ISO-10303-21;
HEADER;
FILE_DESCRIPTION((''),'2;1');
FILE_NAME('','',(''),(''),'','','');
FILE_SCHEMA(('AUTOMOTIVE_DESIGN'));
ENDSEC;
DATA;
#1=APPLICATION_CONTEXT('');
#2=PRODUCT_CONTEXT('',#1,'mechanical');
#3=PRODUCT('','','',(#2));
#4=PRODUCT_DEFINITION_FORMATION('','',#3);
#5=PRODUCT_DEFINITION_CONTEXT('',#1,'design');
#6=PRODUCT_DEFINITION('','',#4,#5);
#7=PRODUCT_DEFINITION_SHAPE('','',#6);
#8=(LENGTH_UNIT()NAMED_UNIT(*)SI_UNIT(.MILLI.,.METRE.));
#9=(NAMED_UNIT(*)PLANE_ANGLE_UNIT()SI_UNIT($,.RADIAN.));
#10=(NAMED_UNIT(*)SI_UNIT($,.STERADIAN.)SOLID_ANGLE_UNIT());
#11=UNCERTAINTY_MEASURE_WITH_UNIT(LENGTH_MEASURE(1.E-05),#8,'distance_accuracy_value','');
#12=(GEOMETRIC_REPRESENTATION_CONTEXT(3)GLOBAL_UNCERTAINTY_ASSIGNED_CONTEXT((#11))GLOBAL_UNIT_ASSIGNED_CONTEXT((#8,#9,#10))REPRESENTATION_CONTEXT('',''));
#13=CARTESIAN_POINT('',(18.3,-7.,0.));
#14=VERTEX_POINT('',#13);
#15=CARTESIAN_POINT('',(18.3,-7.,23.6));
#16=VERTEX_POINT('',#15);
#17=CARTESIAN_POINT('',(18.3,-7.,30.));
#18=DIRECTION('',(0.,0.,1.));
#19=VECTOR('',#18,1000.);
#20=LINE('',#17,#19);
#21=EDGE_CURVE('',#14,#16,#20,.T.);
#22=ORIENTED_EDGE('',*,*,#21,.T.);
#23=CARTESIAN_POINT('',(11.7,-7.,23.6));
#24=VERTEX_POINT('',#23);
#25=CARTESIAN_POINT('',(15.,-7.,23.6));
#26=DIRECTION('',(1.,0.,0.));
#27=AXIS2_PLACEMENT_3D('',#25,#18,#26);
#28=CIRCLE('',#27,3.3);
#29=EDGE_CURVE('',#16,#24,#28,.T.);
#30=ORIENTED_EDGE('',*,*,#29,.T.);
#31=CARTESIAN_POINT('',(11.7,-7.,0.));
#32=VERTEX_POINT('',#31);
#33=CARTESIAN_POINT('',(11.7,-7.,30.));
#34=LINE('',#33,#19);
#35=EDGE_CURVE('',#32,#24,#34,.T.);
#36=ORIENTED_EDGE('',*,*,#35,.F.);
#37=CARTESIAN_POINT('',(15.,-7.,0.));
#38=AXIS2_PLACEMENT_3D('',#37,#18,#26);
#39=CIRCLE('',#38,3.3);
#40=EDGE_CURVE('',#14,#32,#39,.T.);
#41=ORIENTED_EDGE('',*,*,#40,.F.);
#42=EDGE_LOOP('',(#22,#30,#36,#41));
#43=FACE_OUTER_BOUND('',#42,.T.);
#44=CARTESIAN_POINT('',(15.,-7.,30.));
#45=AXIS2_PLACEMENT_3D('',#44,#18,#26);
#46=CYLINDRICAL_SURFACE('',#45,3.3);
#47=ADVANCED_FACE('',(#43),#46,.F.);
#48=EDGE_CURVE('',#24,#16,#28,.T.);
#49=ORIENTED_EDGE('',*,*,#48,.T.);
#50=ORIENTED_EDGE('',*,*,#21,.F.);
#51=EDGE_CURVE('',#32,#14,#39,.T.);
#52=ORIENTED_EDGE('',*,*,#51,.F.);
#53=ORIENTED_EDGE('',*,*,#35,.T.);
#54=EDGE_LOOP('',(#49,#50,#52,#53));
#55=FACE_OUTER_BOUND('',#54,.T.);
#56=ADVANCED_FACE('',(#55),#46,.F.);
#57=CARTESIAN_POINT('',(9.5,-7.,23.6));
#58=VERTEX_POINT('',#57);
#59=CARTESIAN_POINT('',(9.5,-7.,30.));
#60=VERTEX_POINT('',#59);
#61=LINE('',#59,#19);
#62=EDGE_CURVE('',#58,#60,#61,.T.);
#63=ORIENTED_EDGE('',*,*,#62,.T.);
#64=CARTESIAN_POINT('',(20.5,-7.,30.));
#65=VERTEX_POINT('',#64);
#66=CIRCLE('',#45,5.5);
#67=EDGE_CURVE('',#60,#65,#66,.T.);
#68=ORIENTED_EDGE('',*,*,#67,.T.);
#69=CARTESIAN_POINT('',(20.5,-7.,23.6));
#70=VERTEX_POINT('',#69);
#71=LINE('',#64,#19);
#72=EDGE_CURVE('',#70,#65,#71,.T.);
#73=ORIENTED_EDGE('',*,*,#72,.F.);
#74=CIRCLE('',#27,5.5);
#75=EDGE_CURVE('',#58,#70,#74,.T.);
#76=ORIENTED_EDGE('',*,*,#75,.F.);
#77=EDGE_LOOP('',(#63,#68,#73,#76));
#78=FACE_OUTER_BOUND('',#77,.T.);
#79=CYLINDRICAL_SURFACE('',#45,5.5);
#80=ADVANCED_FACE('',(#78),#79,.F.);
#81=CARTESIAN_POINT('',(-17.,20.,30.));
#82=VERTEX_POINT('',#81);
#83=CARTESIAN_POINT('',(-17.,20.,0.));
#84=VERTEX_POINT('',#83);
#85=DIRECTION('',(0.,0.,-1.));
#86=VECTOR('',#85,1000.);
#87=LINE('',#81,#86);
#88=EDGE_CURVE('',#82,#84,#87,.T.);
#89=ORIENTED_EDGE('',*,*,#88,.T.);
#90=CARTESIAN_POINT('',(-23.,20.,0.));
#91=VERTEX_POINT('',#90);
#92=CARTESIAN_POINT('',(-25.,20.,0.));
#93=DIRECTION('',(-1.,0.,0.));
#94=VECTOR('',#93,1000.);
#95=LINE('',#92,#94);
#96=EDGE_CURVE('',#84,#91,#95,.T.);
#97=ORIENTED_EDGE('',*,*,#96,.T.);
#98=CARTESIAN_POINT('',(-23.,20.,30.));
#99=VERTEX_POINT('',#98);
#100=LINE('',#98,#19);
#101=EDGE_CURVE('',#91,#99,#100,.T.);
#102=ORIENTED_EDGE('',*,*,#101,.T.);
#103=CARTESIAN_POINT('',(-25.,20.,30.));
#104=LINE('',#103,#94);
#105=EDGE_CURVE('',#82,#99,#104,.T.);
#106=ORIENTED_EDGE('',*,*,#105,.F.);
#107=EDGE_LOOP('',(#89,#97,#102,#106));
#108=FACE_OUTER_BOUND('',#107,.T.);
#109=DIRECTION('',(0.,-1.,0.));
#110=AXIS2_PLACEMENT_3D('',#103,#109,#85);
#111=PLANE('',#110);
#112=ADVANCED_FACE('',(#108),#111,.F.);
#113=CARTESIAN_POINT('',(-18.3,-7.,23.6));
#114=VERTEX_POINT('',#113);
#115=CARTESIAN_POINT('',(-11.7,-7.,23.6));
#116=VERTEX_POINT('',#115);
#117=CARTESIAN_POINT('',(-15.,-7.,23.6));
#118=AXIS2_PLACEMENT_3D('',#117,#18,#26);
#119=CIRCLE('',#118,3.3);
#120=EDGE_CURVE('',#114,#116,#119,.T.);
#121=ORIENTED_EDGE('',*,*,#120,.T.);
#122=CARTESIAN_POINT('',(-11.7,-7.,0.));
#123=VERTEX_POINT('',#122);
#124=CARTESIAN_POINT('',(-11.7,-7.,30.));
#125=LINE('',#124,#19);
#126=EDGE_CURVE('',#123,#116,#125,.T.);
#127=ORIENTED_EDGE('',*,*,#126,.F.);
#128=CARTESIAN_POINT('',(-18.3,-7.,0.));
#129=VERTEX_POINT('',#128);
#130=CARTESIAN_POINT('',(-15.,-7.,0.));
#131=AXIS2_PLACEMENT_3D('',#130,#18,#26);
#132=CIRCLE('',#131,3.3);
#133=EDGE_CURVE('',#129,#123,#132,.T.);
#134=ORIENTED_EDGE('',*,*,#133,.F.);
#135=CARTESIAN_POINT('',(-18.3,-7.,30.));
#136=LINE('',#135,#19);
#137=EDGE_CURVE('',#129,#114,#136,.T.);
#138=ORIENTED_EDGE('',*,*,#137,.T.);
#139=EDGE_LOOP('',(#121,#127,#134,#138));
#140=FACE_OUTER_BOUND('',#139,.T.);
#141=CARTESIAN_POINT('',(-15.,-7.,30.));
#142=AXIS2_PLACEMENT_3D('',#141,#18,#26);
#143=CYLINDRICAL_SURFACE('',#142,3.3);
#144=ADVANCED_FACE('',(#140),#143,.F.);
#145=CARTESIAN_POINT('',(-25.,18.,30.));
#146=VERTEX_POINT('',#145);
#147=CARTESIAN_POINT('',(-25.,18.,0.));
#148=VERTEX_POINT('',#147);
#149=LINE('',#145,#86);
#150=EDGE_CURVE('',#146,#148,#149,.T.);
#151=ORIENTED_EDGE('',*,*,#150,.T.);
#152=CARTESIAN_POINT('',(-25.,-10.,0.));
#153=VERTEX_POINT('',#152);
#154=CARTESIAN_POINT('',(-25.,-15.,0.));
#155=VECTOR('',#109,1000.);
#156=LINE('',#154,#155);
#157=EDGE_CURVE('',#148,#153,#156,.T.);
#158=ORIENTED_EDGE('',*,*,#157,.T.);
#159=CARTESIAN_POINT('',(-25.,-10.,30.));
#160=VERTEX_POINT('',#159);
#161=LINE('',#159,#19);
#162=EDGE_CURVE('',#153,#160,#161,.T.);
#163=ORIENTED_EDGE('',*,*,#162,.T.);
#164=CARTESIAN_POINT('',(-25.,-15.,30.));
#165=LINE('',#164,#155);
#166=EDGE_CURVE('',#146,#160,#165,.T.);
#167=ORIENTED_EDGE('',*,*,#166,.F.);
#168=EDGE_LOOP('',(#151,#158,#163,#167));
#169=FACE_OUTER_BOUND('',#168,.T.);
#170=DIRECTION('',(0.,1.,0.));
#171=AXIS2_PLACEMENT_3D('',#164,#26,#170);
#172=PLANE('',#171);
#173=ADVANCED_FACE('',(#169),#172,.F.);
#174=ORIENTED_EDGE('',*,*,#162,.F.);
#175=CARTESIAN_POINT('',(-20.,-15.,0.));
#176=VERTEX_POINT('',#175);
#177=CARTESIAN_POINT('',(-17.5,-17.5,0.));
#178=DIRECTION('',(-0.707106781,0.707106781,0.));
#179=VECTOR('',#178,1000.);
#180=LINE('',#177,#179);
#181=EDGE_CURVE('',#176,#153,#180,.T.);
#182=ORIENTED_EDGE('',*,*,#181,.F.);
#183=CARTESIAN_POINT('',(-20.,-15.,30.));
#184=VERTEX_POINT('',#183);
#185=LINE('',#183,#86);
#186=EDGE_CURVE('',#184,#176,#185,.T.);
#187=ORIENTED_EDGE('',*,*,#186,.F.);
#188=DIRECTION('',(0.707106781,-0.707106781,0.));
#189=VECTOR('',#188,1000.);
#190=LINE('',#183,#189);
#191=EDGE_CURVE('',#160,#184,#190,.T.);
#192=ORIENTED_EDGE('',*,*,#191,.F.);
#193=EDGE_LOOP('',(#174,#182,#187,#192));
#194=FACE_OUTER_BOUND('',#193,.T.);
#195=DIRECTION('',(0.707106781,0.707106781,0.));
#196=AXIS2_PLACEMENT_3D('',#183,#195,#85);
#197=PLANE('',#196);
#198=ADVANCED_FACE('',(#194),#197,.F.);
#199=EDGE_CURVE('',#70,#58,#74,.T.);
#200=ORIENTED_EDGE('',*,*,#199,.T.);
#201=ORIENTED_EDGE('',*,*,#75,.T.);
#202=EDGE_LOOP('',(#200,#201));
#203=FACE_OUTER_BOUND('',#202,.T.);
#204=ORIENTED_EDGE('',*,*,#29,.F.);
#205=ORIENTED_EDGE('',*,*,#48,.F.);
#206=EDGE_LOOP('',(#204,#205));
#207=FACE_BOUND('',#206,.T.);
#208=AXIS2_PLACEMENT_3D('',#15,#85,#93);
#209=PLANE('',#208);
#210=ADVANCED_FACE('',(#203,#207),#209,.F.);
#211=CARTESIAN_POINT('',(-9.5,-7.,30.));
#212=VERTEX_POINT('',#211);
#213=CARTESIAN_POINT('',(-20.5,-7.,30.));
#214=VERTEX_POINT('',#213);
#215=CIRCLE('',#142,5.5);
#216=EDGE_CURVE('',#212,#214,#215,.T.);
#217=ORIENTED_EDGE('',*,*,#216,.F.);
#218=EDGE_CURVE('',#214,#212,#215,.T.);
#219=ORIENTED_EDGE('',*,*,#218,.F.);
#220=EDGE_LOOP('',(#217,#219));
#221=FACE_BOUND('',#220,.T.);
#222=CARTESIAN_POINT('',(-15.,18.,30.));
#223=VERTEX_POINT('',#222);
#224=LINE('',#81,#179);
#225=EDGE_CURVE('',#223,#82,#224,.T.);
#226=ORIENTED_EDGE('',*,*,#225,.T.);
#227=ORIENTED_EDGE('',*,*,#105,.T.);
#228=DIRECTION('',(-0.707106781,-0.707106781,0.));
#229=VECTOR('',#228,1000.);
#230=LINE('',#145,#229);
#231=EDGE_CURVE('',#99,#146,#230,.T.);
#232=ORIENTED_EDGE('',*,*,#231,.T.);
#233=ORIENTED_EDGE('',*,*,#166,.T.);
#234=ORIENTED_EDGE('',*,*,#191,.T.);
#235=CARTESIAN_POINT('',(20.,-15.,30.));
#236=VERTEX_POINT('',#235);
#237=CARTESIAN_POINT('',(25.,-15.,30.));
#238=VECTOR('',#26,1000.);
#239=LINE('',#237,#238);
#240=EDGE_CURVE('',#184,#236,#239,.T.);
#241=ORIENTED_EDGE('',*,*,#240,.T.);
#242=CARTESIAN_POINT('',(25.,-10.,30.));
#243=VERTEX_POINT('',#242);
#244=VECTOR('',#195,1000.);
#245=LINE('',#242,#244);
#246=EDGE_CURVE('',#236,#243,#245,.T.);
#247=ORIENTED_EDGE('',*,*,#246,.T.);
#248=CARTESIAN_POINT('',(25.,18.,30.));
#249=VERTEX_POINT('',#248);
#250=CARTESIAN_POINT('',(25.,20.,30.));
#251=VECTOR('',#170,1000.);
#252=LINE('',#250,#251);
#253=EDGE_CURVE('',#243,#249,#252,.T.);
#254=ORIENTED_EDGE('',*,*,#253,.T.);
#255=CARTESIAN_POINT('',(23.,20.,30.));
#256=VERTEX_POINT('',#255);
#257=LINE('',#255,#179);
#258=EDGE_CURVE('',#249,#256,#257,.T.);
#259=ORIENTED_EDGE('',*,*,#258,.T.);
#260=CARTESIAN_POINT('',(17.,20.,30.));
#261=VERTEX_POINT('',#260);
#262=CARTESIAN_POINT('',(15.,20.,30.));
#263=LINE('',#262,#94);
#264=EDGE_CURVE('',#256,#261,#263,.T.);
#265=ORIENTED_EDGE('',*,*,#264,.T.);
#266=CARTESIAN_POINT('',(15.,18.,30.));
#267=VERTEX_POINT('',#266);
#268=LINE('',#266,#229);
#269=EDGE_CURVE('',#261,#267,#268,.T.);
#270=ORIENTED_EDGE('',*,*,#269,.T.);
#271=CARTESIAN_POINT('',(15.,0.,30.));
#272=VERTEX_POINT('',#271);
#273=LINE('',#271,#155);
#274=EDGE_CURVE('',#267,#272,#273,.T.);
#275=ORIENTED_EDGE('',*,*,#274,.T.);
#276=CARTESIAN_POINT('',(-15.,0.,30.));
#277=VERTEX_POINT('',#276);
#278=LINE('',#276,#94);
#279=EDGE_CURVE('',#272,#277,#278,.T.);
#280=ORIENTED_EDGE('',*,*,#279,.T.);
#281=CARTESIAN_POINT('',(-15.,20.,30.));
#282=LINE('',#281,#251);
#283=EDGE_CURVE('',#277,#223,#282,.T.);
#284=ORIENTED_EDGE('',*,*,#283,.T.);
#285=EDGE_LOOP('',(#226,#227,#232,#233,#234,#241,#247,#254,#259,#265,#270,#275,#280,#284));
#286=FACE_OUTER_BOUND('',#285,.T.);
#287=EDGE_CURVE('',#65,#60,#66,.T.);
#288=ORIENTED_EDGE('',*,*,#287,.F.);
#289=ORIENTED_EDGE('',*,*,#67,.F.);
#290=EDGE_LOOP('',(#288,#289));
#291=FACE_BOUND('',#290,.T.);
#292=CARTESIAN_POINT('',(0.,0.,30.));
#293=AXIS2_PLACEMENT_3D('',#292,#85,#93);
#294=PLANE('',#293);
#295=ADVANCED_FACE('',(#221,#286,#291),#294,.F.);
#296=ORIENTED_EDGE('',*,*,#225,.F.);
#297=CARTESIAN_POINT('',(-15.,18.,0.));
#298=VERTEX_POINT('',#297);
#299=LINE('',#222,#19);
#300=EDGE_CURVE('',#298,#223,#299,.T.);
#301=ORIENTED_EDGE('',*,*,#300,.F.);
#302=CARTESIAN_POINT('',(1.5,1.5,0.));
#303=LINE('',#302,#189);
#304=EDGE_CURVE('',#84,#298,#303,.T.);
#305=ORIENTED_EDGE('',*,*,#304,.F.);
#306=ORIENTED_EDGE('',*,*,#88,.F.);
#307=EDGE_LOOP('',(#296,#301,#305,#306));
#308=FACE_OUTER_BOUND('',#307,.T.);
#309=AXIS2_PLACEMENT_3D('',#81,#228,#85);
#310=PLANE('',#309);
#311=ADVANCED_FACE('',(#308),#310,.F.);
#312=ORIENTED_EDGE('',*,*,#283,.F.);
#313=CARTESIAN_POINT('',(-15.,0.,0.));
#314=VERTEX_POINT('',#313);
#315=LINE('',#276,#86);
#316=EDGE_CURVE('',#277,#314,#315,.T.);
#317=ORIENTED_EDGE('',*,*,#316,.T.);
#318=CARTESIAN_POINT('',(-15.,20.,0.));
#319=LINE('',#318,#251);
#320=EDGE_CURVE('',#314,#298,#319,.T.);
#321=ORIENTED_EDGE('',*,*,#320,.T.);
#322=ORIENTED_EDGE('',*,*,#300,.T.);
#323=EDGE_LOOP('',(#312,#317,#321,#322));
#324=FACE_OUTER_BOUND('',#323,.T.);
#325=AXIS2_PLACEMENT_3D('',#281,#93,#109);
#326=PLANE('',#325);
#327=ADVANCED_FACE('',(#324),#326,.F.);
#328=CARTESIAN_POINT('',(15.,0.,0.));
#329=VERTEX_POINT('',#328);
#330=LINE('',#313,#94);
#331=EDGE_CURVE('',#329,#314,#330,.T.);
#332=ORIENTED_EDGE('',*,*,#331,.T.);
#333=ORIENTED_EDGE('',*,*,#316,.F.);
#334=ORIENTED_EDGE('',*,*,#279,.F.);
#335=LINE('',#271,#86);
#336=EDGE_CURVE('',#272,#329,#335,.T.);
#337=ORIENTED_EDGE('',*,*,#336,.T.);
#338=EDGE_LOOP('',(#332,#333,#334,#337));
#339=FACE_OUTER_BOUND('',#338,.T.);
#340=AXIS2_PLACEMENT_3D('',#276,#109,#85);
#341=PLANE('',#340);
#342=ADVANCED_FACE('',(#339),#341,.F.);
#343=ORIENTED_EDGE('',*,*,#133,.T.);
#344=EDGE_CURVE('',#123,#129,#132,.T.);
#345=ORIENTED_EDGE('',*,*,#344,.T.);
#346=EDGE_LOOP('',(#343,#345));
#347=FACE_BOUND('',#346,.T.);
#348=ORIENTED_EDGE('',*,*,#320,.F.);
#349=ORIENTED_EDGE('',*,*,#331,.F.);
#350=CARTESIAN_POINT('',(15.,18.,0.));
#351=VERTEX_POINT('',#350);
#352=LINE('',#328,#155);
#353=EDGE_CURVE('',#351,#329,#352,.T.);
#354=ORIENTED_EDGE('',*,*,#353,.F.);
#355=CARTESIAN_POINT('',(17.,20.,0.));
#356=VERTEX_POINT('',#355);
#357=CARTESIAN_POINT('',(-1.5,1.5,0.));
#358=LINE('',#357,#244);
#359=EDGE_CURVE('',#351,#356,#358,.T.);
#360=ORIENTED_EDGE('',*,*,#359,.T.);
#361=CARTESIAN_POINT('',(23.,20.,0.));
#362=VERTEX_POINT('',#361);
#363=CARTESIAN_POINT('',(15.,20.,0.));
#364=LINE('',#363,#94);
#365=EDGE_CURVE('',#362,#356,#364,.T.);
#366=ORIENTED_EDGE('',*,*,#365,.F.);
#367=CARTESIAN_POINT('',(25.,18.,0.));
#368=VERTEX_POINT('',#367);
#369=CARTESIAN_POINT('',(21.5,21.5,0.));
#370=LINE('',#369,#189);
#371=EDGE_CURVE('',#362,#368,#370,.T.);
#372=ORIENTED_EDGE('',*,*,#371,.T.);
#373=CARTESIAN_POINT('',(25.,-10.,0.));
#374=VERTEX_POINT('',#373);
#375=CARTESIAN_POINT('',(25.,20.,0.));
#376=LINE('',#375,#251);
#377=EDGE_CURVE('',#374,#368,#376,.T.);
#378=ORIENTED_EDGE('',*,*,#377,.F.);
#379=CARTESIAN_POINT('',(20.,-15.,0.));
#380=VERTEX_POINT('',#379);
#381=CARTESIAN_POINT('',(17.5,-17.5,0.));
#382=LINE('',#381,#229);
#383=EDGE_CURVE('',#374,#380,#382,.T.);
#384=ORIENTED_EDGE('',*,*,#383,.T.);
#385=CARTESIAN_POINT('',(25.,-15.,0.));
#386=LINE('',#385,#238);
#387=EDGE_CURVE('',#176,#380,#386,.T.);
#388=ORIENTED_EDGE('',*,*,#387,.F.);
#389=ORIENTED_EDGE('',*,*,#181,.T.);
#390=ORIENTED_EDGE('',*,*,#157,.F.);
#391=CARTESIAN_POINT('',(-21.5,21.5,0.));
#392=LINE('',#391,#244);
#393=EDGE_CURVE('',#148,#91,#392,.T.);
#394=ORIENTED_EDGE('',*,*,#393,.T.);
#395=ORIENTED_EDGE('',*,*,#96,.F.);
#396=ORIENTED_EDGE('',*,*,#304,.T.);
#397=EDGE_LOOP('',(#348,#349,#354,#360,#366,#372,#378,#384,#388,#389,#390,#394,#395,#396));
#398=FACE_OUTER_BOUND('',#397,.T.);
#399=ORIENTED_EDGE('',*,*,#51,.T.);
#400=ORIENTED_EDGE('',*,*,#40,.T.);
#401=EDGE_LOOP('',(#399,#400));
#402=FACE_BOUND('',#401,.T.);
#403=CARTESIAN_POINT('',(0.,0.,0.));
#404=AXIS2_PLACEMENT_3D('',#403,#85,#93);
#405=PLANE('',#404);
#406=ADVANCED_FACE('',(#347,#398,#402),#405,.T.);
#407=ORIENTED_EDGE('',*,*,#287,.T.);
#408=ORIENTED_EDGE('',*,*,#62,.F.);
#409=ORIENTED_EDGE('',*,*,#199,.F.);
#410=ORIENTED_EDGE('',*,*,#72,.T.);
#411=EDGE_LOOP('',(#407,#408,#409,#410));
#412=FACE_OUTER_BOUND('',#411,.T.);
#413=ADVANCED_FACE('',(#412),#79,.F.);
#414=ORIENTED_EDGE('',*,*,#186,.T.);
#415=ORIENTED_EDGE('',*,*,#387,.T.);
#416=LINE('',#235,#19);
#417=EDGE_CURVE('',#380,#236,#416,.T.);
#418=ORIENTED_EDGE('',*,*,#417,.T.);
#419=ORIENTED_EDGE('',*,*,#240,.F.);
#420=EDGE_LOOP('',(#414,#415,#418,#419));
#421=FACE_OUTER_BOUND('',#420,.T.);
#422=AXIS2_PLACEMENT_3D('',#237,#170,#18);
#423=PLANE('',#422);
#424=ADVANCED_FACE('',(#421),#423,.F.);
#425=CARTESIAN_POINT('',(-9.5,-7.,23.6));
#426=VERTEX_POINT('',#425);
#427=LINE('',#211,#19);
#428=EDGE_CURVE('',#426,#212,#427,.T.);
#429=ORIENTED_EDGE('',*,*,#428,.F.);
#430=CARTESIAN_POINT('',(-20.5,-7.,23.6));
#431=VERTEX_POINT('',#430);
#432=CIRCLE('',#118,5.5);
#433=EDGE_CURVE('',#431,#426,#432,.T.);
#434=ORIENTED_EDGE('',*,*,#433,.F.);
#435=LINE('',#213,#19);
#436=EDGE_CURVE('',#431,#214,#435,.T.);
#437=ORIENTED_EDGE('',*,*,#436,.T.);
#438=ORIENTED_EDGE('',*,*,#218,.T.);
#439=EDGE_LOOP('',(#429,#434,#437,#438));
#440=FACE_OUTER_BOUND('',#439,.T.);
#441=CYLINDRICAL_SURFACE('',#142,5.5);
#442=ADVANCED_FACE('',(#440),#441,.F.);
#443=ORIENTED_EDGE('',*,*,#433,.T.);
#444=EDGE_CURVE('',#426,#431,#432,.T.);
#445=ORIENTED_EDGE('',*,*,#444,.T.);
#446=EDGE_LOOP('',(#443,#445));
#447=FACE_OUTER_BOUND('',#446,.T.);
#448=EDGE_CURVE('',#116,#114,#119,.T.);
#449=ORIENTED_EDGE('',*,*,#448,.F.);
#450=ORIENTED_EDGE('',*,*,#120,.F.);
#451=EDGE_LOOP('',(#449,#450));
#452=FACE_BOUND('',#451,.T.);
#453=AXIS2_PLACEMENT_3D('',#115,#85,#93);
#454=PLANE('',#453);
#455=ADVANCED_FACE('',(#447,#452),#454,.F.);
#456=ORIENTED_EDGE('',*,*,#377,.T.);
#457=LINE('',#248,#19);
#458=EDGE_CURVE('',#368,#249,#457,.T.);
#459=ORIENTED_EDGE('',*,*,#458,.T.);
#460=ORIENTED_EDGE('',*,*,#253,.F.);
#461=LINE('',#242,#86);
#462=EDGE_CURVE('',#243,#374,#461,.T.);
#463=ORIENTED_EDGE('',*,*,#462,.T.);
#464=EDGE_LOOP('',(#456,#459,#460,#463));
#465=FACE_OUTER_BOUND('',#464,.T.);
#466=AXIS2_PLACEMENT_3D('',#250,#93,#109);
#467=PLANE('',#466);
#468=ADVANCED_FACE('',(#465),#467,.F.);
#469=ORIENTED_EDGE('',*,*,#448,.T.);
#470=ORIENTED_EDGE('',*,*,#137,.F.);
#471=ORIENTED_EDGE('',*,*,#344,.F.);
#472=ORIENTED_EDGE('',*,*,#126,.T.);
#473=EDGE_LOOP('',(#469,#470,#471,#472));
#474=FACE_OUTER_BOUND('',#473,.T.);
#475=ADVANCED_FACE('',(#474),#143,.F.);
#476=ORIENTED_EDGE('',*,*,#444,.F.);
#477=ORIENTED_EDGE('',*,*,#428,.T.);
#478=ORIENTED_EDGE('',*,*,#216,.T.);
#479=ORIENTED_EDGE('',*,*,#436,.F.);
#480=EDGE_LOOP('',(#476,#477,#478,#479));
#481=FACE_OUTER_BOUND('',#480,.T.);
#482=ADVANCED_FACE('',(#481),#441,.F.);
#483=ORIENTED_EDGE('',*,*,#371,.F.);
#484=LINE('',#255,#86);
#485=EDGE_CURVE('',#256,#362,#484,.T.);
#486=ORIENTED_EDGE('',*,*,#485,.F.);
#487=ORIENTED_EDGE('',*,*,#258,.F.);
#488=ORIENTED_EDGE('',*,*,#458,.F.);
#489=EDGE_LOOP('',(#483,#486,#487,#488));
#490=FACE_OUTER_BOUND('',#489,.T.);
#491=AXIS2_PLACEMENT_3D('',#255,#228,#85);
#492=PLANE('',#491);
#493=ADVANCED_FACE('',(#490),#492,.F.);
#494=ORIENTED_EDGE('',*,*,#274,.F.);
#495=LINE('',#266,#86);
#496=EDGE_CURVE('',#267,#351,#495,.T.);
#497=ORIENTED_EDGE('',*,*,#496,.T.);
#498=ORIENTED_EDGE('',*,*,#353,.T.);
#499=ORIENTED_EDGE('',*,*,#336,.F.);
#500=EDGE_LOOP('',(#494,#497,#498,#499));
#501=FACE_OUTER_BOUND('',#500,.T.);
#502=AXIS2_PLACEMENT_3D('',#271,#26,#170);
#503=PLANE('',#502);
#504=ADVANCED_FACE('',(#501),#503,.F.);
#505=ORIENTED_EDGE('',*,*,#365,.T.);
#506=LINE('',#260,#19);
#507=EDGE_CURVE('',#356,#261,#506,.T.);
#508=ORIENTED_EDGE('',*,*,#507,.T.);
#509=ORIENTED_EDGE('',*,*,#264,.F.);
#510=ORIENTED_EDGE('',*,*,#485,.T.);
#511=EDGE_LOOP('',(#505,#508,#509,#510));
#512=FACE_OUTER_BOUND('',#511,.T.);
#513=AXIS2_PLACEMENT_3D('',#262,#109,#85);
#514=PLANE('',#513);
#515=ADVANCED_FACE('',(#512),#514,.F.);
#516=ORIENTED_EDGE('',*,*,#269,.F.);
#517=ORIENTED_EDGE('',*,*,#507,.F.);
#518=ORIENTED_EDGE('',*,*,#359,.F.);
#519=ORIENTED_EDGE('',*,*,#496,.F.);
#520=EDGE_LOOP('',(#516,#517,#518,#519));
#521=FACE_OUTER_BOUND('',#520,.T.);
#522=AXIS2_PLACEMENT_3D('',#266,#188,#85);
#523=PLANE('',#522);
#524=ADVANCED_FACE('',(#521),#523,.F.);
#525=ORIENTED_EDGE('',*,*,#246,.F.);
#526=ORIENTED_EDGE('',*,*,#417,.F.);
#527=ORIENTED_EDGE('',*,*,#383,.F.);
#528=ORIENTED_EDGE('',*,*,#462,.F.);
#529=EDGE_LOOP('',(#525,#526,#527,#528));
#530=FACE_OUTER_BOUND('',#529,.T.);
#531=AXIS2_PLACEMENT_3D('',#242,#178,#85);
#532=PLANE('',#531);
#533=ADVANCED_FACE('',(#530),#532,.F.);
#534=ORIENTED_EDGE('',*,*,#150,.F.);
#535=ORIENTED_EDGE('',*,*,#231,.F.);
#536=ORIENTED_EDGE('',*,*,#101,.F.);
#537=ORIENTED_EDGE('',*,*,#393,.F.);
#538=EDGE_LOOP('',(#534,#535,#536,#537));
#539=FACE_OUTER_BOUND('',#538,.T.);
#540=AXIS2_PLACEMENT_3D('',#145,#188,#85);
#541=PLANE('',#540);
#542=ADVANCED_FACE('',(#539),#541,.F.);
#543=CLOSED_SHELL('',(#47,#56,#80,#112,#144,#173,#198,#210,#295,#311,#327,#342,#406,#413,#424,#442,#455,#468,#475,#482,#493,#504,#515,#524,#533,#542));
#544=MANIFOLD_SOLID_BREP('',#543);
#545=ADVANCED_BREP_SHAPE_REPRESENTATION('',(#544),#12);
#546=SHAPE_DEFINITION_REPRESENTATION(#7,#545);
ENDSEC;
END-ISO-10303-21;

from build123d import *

# Parameters (mm, degrees)
BOSS_EXTRUDE1_DEPTH                                 = 30
CBORE_FOR_M6_HEX_SOCKET_HEAD_CAP_SCREW1_D           = 6.6
CBORE_FOR_M6_HEX_SOCKET_HEAD_CAP_SCREW1_CBORE_D     = 11
CBORE_FOR_M6_HEX_SOCKET_HEAD_CAP_SCREW1_CBORE_DEPTH = 6.4
CHAMFER1_SIZE                                       = 2
CHAMFER2_SIZE                                       = 5


with BuildPart() as part:
    # Sketch1 → Boss-Extrude1 (new body)
    with BuildSketch(Plane.XY):
        Polygon((-25, 20), (-15, 20), (-15, 0), (15, 0), (15, 20), (25, 20), (25, -15), (-25, -15), align=None)
    extrude(amount=BOSS_EXTRUDE1_DEPTH)

    # CBORE for M6 Hex Socket Head Cap Screw1 (through all)
    with Locations(Plane.XY.offset(30)):
        with Locations((-15, -7), (15, -7)):
            CounterBoreHole(CBORE_FOR_M6_HEX_SOCKET_HEAD_CAP_SCREW1_D / 2, CBORE_FOR_M6_HEX_SOCKET_HEAD_CAP_SCREW1_CBORE_D / 2, CBORE_FOR_M6_HEX_SOCKET_HEAD_CAP_SCREW1_CBORE_DEPTH)

    # Chamfer1
    chamfer1_edges = [part.edges().sort_by_distance(p)[0] for p in [
        (-25, 20, 15),
        (-15, 20, 15),
        (15, 20, 15),
        (25, 20, 15),
    ]]
    chamfer(chamfer1_edges, length=CHAMFER1_SIZE)

    # Chamfer2
    chamfer2_edges = [part.edges().sort_by_distance(p)[0] for p in [
        (25, -15, 15),
        (-25, -15, 15),
    ]]
    chamfer(chamfer2_edges, length=CHAMFER2_SIZE)


solid = part.part
